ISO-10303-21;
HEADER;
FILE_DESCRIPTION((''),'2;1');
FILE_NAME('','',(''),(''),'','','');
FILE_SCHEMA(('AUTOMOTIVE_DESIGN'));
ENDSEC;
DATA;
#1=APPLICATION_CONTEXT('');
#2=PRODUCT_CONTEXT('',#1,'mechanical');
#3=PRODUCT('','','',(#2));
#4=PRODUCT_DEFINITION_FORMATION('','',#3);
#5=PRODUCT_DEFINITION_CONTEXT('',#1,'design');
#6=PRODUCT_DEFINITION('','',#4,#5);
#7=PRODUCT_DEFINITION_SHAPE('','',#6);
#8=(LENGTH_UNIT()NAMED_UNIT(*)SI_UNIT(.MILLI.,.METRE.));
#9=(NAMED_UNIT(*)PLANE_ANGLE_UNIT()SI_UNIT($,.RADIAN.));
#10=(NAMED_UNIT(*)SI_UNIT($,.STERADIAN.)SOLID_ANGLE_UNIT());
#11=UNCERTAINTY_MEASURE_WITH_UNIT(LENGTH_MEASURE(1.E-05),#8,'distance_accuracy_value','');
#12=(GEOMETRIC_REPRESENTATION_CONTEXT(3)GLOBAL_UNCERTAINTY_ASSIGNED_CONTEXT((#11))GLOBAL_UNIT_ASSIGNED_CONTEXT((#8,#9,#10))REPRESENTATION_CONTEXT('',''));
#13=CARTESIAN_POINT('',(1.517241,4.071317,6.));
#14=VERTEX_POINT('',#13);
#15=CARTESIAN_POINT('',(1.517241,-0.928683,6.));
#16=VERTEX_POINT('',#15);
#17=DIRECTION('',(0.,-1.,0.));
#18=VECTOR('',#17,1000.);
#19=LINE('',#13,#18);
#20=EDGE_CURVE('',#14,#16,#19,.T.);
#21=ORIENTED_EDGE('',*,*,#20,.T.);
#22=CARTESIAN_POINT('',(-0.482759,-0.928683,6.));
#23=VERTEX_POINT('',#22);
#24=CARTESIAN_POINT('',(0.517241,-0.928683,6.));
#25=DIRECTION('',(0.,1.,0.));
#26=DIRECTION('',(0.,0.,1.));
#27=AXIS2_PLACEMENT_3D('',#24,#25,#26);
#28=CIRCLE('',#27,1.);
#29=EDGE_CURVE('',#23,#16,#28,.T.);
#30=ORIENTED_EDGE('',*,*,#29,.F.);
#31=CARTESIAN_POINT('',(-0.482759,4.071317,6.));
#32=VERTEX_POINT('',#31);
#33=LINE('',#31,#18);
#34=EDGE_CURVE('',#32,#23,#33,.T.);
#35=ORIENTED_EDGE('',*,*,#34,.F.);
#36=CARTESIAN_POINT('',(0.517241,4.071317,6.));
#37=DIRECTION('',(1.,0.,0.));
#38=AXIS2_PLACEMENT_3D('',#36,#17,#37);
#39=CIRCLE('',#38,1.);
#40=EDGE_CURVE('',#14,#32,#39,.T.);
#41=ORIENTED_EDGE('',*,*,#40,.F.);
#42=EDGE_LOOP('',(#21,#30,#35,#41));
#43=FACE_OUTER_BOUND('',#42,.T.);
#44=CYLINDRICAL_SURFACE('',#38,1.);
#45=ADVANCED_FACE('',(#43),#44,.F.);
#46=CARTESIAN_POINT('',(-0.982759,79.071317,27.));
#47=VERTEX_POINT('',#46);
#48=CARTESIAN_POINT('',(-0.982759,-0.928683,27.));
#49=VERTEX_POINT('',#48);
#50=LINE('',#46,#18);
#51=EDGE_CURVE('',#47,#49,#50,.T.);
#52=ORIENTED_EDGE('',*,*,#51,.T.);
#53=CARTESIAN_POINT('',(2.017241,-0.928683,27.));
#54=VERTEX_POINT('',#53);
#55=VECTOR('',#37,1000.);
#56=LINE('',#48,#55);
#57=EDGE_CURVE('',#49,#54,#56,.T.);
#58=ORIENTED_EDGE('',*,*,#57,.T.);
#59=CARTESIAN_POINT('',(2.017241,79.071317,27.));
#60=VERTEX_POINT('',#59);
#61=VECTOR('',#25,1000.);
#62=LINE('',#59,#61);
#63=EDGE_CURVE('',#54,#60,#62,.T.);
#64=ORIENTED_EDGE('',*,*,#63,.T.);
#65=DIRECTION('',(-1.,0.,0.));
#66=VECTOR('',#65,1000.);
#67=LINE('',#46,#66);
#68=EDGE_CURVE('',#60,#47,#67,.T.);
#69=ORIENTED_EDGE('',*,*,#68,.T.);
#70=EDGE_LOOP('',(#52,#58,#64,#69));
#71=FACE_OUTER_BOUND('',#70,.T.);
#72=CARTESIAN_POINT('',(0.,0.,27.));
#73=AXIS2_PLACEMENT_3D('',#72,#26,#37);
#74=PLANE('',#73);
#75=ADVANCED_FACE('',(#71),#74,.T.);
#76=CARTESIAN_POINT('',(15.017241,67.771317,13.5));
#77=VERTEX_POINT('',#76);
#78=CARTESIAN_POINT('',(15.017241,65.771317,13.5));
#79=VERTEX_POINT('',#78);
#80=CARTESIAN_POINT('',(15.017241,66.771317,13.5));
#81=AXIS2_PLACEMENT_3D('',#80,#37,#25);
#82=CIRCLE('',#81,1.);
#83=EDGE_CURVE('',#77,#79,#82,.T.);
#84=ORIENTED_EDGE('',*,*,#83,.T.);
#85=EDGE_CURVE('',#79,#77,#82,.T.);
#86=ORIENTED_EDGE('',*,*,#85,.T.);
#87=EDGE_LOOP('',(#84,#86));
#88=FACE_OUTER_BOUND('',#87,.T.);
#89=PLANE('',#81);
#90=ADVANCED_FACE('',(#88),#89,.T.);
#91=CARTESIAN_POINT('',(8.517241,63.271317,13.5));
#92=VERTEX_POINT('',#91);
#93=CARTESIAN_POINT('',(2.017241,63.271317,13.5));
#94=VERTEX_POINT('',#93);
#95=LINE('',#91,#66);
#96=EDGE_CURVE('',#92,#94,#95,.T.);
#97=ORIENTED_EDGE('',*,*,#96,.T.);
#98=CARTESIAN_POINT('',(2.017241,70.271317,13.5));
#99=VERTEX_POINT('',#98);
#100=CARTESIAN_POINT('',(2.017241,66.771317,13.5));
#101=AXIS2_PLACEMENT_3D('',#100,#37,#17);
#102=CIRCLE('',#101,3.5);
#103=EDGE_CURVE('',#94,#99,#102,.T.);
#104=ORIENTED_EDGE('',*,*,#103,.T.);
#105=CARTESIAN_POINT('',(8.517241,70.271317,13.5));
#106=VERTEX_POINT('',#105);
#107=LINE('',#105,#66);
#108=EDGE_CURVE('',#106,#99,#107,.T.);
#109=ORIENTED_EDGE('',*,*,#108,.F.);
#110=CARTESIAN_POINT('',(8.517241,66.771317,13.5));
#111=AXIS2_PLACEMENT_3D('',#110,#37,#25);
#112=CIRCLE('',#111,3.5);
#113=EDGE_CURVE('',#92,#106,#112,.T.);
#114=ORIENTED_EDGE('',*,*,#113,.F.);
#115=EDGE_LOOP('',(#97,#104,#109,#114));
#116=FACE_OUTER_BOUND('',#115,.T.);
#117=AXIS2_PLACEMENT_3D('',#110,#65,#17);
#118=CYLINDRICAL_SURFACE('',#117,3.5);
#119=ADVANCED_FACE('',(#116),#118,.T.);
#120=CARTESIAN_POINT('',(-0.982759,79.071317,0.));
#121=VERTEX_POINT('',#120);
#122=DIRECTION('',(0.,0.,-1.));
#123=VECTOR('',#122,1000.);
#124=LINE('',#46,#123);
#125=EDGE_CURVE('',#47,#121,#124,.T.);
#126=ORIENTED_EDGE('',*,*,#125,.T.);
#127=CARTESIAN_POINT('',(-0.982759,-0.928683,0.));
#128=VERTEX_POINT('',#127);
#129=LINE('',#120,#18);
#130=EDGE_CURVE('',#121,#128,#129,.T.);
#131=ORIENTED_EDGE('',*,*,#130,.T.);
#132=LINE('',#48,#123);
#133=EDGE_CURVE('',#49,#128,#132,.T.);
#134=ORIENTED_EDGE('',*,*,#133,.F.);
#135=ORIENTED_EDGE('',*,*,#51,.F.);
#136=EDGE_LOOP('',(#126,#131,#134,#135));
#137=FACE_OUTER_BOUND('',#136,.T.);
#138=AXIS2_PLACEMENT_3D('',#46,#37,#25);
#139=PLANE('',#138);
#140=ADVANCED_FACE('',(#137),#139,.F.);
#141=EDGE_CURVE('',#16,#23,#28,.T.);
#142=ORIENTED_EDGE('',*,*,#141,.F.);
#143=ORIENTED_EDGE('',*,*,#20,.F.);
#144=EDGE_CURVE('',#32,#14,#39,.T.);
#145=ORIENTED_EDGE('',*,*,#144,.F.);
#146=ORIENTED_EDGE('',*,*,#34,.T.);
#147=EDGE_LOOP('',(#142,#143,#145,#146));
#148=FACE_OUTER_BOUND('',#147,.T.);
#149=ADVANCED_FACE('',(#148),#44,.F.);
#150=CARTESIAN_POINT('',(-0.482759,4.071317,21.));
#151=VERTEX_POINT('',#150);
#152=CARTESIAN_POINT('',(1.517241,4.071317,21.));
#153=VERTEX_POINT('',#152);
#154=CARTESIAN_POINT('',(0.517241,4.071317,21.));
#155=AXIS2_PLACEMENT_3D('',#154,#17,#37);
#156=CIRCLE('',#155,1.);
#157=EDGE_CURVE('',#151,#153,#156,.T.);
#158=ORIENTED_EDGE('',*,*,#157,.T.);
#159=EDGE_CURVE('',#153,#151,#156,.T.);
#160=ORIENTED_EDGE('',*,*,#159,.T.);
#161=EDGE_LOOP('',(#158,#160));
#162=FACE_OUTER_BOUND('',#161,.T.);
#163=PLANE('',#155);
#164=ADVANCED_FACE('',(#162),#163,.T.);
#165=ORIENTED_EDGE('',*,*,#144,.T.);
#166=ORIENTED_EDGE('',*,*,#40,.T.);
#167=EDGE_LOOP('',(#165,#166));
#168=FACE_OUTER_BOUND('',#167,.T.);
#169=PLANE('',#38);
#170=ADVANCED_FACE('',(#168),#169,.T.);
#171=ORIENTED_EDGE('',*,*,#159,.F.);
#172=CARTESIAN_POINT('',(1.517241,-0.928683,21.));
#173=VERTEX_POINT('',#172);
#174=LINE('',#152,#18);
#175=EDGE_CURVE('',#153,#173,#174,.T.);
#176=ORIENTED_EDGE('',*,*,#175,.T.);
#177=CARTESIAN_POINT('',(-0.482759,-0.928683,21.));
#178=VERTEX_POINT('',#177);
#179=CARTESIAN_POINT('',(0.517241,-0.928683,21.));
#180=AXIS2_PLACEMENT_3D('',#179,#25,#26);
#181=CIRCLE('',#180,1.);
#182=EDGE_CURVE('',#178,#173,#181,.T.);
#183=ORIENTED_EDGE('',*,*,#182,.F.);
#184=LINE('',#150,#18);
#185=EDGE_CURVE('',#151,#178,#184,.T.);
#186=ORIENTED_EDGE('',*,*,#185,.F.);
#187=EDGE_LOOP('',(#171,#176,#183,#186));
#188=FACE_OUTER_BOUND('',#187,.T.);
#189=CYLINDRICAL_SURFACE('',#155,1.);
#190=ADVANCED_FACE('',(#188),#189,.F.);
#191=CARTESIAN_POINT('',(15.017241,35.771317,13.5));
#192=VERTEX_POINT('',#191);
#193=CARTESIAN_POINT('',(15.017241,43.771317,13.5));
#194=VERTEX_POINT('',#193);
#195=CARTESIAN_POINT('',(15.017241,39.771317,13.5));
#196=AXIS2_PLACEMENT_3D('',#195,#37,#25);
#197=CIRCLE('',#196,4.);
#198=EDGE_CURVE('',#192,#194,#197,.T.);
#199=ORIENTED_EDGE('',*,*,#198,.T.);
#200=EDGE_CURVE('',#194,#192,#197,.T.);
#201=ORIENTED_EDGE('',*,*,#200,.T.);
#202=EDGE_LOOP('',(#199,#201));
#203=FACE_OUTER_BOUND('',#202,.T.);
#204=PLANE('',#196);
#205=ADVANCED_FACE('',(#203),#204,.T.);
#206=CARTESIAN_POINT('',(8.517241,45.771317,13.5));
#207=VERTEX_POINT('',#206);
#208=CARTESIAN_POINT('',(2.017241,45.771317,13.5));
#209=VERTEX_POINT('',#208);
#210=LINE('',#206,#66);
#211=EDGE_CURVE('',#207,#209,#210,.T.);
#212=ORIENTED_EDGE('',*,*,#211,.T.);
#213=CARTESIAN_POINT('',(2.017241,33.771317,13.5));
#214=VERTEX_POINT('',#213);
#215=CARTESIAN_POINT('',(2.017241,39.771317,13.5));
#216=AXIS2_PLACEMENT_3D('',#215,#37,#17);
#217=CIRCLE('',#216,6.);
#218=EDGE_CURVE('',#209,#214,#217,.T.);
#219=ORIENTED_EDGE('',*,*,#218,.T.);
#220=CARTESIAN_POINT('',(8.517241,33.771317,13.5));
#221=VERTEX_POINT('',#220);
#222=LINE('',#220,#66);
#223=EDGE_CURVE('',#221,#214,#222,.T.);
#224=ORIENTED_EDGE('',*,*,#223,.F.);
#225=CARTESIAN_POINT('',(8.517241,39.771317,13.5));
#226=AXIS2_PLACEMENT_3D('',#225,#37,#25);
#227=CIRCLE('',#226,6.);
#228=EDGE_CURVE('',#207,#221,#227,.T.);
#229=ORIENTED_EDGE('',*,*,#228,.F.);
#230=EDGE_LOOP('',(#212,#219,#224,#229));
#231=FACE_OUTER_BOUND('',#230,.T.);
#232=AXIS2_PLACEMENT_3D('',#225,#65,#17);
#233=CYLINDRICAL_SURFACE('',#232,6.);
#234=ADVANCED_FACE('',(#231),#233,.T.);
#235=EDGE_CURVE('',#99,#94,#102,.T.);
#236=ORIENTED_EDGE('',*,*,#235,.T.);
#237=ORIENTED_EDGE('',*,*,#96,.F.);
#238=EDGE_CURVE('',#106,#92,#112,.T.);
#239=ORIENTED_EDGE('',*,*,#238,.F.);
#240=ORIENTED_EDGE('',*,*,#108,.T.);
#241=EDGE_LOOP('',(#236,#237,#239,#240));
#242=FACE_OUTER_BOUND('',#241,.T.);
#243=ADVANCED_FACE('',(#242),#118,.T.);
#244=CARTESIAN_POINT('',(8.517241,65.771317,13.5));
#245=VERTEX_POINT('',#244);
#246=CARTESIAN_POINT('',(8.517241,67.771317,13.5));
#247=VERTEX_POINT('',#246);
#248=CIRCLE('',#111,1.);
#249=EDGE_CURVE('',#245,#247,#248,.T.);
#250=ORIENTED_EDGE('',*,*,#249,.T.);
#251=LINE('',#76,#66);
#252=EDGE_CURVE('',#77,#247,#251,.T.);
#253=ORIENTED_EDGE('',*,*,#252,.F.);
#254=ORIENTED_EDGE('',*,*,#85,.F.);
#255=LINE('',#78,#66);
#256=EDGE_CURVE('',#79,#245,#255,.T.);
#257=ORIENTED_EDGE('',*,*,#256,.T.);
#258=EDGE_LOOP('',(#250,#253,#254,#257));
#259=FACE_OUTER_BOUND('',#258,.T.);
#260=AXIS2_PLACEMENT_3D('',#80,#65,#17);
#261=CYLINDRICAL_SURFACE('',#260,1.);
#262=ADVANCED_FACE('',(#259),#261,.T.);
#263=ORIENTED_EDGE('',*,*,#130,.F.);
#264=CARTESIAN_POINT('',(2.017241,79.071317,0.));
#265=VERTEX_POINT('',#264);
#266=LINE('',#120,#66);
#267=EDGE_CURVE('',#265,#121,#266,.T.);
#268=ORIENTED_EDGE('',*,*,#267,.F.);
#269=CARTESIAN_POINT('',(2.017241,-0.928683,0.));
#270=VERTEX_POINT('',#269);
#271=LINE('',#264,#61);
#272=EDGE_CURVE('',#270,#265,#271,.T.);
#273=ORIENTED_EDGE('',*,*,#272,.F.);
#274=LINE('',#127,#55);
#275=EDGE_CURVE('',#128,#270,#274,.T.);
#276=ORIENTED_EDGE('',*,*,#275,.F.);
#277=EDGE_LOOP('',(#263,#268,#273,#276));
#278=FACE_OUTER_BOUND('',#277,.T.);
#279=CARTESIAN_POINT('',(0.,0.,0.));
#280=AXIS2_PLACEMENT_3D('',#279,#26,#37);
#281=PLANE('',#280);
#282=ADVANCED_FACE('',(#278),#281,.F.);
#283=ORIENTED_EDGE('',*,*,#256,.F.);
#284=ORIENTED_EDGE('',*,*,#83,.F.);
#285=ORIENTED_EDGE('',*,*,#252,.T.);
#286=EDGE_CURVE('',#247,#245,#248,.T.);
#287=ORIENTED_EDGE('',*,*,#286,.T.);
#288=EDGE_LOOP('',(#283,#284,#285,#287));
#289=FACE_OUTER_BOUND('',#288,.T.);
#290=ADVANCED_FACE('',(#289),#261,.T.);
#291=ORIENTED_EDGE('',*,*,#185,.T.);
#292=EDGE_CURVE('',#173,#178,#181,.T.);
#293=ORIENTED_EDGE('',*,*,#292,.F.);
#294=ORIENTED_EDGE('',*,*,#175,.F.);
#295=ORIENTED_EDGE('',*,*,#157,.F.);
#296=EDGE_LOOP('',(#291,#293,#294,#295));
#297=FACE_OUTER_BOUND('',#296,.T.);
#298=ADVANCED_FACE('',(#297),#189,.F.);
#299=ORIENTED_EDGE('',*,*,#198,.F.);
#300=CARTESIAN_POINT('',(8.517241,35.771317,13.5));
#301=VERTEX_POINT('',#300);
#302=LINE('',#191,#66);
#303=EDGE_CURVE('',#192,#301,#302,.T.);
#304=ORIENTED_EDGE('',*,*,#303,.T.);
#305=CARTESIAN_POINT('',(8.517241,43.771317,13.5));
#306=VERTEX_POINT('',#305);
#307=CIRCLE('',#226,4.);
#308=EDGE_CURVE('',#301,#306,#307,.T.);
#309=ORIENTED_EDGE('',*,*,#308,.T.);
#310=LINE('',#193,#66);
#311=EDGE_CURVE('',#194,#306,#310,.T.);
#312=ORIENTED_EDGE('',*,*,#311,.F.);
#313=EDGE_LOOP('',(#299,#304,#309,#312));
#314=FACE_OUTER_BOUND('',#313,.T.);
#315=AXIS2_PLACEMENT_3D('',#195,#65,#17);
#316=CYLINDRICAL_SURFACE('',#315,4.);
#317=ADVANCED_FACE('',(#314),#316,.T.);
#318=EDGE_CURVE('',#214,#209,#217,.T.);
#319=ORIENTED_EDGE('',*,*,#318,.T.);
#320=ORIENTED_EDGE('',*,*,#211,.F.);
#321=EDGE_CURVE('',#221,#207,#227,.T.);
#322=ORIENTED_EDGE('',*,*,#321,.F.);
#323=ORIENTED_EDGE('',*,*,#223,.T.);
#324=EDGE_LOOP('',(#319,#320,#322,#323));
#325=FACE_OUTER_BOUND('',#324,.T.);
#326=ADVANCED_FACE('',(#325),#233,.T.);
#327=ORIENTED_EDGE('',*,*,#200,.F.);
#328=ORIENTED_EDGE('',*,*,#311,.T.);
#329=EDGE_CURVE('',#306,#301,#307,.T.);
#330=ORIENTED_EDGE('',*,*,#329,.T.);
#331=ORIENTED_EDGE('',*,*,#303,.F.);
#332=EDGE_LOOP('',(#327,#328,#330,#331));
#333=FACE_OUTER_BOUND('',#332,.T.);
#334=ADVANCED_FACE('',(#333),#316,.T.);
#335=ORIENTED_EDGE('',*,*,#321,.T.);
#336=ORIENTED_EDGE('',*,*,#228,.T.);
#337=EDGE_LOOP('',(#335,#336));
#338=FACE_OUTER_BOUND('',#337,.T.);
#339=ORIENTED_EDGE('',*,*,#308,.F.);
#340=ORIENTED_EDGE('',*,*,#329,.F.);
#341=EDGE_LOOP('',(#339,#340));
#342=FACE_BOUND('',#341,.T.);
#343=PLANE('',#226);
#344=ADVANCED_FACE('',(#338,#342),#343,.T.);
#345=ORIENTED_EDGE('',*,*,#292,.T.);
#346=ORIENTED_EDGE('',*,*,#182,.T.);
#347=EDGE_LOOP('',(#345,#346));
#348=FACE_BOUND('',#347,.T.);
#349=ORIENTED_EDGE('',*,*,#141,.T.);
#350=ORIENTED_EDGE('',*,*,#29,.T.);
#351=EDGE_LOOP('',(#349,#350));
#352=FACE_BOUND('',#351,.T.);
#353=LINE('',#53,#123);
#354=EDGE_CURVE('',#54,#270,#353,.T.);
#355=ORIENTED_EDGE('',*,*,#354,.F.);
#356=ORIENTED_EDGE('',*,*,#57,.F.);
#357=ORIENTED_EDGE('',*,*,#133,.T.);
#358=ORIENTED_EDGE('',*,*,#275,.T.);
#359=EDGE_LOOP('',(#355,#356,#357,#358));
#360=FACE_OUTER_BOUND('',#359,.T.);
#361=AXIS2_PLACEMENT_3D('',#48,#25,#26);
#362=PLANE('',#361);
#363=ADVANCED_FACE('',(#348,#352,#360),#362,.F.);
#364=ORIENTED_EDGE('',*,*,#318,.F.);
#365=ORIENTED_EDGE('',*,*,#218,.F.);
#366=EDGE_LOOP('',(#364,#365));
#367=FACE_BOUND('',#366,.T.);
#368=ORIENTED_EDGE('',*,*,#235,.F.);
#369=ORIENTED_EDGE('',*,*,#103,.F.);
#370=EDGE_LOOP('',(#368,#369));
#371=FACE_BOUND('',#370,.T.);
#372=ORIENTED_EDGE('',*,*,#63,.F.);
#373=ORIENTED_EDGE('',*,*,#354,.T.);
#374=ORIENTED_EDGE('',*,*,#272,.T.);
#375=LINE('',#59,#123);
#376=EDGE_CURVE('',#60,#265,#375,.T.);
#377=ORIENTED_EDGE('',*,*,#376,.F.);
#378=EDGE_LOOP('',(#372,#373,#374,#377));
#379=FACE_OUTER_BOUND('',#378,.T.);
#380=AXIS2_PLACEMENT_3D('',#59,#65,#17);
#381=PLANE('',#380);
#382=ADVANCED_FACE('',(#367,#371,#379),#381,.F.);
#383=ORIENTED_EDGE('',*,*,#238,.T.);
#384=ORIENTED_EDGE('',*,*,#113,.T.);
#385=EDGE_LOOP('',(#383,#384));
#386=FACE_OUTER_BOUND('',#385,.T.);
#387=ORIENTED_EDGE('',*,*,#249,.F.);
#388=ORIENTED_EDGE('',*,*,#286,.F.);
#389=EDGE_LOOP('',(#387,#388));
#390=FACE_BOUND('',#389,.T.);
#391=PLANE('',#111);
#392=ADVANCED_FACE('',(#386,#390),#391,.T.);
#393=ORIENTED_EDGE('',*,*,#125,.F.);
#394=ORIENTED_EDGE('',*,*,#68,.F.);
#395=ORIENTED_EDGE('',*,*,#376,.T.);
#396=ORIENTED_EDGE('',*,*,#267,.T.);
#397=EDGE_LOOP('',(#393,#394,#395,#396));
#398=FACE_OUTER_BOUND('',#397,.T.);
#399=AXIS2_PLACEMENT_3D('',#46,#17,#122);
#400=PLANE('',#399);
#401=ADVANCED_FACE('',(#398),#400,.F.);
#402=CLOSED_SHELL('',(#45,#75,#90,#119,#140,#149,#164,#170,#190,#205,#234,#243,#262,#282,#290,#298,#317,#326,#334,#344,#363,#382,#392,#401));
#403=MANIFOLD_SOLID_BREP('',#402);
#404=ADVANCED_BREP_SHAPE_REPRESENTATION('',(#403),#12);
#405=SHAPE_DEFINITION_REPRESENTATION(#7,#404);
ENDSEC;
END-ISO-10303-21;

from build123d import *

# Parameters (mm, degrees)
SKETCH_1_W          = 3
SKETCH_1_H          = 80
EXTRUDE_1_DEPTH     = 27
SKETCH_2_R          = 3.5
SKETCH_2_R_2        = 6
EXTRUDE_2_DEPTH     = 6.5
SKETCH_3_R          = 1
SKETCH_3_R_2        = 4
EXTRUDE_3_DEPTH     = 6.5
SKETCH_4_R          = 1
CUT_EXTRUDE_1_DEPTH = 15


with BuildPart() as part:
    # 草图1 → 凸台-拉伸1 (new body)
    with BuildSketch(Plane.XY):
        with Locations((0.517241379, 39.071316614)):
            Rectangle(SKETCH_1_W, SKETCH_1_H)
    extrude(amount=EXTRUDE_1_DEPTH)

    # 草图2 → 凸台-拉伸2 (add)
    with BuildSketch(Plane(origin=(2.017241379, 0, 0), x_dir=(0, 0, -1), z_dir=(1, 0, 0))):
        with Locations(Location((-13.5, 66.771316614, 0), (0, 0, 270))):
            Circle(SKETCH_2_R)
        with Locations(Location((-13.5, 39.771316614, 0), (0, 0, 270))):
            Circle(SKETCH_2_R_2)
    extrude(amount=EXTRUDE_2_DEPTH)

    # 草图3 → 凸台-拉伸3 (add)
    with BuildSketch(Plane(origin=(8.517241379, 0, 0), x_dir=(0, 0, -1), z_dir=(1, 0, 0))):
        with Locations(Location((-13.5, 66.771316614, 0), (0, 0, 270))):
            Circle(SKETCH_3_R)
        with Locations(Location((-13.5, 39.771316614, 0), (0, 0, 270))):
            Circle(SKETCH_3_R_2)
    extrude(amount=EXTRUDE_3_DEPTH)

    # 草图4 → 切除-拉伸1 (cut)
    with BuildSketch(Plane(origin=(-1096.213929055, -10.928683386, 855.0606199), x_dir=(0.12186934340512692, -2.2319547324357124e-14, -0.9925461516413246), z_dir=(0, -1, 0))):
        with Locations((963.085867609, 999.8129825)):
            Circle(SKETCH_4_R)
        with Locations((977.974059883, 997.984942349)):
            Circle(SKETCH_4_R)
        with Locations(Location((961.501566145, 986.909882529, 0), (0, 0, 83))):
            Circle(SKETCH_4_R)
        with Locations(Location((976.389758419, 985.081842378, 0), (0, 0, 83))):
            Circle(SKETCH_4_R)
    extrude(amount=-CUT_EXTRUDE_1_DEPTH, mode=Mode.SUBTRACT)


solid = part.part
